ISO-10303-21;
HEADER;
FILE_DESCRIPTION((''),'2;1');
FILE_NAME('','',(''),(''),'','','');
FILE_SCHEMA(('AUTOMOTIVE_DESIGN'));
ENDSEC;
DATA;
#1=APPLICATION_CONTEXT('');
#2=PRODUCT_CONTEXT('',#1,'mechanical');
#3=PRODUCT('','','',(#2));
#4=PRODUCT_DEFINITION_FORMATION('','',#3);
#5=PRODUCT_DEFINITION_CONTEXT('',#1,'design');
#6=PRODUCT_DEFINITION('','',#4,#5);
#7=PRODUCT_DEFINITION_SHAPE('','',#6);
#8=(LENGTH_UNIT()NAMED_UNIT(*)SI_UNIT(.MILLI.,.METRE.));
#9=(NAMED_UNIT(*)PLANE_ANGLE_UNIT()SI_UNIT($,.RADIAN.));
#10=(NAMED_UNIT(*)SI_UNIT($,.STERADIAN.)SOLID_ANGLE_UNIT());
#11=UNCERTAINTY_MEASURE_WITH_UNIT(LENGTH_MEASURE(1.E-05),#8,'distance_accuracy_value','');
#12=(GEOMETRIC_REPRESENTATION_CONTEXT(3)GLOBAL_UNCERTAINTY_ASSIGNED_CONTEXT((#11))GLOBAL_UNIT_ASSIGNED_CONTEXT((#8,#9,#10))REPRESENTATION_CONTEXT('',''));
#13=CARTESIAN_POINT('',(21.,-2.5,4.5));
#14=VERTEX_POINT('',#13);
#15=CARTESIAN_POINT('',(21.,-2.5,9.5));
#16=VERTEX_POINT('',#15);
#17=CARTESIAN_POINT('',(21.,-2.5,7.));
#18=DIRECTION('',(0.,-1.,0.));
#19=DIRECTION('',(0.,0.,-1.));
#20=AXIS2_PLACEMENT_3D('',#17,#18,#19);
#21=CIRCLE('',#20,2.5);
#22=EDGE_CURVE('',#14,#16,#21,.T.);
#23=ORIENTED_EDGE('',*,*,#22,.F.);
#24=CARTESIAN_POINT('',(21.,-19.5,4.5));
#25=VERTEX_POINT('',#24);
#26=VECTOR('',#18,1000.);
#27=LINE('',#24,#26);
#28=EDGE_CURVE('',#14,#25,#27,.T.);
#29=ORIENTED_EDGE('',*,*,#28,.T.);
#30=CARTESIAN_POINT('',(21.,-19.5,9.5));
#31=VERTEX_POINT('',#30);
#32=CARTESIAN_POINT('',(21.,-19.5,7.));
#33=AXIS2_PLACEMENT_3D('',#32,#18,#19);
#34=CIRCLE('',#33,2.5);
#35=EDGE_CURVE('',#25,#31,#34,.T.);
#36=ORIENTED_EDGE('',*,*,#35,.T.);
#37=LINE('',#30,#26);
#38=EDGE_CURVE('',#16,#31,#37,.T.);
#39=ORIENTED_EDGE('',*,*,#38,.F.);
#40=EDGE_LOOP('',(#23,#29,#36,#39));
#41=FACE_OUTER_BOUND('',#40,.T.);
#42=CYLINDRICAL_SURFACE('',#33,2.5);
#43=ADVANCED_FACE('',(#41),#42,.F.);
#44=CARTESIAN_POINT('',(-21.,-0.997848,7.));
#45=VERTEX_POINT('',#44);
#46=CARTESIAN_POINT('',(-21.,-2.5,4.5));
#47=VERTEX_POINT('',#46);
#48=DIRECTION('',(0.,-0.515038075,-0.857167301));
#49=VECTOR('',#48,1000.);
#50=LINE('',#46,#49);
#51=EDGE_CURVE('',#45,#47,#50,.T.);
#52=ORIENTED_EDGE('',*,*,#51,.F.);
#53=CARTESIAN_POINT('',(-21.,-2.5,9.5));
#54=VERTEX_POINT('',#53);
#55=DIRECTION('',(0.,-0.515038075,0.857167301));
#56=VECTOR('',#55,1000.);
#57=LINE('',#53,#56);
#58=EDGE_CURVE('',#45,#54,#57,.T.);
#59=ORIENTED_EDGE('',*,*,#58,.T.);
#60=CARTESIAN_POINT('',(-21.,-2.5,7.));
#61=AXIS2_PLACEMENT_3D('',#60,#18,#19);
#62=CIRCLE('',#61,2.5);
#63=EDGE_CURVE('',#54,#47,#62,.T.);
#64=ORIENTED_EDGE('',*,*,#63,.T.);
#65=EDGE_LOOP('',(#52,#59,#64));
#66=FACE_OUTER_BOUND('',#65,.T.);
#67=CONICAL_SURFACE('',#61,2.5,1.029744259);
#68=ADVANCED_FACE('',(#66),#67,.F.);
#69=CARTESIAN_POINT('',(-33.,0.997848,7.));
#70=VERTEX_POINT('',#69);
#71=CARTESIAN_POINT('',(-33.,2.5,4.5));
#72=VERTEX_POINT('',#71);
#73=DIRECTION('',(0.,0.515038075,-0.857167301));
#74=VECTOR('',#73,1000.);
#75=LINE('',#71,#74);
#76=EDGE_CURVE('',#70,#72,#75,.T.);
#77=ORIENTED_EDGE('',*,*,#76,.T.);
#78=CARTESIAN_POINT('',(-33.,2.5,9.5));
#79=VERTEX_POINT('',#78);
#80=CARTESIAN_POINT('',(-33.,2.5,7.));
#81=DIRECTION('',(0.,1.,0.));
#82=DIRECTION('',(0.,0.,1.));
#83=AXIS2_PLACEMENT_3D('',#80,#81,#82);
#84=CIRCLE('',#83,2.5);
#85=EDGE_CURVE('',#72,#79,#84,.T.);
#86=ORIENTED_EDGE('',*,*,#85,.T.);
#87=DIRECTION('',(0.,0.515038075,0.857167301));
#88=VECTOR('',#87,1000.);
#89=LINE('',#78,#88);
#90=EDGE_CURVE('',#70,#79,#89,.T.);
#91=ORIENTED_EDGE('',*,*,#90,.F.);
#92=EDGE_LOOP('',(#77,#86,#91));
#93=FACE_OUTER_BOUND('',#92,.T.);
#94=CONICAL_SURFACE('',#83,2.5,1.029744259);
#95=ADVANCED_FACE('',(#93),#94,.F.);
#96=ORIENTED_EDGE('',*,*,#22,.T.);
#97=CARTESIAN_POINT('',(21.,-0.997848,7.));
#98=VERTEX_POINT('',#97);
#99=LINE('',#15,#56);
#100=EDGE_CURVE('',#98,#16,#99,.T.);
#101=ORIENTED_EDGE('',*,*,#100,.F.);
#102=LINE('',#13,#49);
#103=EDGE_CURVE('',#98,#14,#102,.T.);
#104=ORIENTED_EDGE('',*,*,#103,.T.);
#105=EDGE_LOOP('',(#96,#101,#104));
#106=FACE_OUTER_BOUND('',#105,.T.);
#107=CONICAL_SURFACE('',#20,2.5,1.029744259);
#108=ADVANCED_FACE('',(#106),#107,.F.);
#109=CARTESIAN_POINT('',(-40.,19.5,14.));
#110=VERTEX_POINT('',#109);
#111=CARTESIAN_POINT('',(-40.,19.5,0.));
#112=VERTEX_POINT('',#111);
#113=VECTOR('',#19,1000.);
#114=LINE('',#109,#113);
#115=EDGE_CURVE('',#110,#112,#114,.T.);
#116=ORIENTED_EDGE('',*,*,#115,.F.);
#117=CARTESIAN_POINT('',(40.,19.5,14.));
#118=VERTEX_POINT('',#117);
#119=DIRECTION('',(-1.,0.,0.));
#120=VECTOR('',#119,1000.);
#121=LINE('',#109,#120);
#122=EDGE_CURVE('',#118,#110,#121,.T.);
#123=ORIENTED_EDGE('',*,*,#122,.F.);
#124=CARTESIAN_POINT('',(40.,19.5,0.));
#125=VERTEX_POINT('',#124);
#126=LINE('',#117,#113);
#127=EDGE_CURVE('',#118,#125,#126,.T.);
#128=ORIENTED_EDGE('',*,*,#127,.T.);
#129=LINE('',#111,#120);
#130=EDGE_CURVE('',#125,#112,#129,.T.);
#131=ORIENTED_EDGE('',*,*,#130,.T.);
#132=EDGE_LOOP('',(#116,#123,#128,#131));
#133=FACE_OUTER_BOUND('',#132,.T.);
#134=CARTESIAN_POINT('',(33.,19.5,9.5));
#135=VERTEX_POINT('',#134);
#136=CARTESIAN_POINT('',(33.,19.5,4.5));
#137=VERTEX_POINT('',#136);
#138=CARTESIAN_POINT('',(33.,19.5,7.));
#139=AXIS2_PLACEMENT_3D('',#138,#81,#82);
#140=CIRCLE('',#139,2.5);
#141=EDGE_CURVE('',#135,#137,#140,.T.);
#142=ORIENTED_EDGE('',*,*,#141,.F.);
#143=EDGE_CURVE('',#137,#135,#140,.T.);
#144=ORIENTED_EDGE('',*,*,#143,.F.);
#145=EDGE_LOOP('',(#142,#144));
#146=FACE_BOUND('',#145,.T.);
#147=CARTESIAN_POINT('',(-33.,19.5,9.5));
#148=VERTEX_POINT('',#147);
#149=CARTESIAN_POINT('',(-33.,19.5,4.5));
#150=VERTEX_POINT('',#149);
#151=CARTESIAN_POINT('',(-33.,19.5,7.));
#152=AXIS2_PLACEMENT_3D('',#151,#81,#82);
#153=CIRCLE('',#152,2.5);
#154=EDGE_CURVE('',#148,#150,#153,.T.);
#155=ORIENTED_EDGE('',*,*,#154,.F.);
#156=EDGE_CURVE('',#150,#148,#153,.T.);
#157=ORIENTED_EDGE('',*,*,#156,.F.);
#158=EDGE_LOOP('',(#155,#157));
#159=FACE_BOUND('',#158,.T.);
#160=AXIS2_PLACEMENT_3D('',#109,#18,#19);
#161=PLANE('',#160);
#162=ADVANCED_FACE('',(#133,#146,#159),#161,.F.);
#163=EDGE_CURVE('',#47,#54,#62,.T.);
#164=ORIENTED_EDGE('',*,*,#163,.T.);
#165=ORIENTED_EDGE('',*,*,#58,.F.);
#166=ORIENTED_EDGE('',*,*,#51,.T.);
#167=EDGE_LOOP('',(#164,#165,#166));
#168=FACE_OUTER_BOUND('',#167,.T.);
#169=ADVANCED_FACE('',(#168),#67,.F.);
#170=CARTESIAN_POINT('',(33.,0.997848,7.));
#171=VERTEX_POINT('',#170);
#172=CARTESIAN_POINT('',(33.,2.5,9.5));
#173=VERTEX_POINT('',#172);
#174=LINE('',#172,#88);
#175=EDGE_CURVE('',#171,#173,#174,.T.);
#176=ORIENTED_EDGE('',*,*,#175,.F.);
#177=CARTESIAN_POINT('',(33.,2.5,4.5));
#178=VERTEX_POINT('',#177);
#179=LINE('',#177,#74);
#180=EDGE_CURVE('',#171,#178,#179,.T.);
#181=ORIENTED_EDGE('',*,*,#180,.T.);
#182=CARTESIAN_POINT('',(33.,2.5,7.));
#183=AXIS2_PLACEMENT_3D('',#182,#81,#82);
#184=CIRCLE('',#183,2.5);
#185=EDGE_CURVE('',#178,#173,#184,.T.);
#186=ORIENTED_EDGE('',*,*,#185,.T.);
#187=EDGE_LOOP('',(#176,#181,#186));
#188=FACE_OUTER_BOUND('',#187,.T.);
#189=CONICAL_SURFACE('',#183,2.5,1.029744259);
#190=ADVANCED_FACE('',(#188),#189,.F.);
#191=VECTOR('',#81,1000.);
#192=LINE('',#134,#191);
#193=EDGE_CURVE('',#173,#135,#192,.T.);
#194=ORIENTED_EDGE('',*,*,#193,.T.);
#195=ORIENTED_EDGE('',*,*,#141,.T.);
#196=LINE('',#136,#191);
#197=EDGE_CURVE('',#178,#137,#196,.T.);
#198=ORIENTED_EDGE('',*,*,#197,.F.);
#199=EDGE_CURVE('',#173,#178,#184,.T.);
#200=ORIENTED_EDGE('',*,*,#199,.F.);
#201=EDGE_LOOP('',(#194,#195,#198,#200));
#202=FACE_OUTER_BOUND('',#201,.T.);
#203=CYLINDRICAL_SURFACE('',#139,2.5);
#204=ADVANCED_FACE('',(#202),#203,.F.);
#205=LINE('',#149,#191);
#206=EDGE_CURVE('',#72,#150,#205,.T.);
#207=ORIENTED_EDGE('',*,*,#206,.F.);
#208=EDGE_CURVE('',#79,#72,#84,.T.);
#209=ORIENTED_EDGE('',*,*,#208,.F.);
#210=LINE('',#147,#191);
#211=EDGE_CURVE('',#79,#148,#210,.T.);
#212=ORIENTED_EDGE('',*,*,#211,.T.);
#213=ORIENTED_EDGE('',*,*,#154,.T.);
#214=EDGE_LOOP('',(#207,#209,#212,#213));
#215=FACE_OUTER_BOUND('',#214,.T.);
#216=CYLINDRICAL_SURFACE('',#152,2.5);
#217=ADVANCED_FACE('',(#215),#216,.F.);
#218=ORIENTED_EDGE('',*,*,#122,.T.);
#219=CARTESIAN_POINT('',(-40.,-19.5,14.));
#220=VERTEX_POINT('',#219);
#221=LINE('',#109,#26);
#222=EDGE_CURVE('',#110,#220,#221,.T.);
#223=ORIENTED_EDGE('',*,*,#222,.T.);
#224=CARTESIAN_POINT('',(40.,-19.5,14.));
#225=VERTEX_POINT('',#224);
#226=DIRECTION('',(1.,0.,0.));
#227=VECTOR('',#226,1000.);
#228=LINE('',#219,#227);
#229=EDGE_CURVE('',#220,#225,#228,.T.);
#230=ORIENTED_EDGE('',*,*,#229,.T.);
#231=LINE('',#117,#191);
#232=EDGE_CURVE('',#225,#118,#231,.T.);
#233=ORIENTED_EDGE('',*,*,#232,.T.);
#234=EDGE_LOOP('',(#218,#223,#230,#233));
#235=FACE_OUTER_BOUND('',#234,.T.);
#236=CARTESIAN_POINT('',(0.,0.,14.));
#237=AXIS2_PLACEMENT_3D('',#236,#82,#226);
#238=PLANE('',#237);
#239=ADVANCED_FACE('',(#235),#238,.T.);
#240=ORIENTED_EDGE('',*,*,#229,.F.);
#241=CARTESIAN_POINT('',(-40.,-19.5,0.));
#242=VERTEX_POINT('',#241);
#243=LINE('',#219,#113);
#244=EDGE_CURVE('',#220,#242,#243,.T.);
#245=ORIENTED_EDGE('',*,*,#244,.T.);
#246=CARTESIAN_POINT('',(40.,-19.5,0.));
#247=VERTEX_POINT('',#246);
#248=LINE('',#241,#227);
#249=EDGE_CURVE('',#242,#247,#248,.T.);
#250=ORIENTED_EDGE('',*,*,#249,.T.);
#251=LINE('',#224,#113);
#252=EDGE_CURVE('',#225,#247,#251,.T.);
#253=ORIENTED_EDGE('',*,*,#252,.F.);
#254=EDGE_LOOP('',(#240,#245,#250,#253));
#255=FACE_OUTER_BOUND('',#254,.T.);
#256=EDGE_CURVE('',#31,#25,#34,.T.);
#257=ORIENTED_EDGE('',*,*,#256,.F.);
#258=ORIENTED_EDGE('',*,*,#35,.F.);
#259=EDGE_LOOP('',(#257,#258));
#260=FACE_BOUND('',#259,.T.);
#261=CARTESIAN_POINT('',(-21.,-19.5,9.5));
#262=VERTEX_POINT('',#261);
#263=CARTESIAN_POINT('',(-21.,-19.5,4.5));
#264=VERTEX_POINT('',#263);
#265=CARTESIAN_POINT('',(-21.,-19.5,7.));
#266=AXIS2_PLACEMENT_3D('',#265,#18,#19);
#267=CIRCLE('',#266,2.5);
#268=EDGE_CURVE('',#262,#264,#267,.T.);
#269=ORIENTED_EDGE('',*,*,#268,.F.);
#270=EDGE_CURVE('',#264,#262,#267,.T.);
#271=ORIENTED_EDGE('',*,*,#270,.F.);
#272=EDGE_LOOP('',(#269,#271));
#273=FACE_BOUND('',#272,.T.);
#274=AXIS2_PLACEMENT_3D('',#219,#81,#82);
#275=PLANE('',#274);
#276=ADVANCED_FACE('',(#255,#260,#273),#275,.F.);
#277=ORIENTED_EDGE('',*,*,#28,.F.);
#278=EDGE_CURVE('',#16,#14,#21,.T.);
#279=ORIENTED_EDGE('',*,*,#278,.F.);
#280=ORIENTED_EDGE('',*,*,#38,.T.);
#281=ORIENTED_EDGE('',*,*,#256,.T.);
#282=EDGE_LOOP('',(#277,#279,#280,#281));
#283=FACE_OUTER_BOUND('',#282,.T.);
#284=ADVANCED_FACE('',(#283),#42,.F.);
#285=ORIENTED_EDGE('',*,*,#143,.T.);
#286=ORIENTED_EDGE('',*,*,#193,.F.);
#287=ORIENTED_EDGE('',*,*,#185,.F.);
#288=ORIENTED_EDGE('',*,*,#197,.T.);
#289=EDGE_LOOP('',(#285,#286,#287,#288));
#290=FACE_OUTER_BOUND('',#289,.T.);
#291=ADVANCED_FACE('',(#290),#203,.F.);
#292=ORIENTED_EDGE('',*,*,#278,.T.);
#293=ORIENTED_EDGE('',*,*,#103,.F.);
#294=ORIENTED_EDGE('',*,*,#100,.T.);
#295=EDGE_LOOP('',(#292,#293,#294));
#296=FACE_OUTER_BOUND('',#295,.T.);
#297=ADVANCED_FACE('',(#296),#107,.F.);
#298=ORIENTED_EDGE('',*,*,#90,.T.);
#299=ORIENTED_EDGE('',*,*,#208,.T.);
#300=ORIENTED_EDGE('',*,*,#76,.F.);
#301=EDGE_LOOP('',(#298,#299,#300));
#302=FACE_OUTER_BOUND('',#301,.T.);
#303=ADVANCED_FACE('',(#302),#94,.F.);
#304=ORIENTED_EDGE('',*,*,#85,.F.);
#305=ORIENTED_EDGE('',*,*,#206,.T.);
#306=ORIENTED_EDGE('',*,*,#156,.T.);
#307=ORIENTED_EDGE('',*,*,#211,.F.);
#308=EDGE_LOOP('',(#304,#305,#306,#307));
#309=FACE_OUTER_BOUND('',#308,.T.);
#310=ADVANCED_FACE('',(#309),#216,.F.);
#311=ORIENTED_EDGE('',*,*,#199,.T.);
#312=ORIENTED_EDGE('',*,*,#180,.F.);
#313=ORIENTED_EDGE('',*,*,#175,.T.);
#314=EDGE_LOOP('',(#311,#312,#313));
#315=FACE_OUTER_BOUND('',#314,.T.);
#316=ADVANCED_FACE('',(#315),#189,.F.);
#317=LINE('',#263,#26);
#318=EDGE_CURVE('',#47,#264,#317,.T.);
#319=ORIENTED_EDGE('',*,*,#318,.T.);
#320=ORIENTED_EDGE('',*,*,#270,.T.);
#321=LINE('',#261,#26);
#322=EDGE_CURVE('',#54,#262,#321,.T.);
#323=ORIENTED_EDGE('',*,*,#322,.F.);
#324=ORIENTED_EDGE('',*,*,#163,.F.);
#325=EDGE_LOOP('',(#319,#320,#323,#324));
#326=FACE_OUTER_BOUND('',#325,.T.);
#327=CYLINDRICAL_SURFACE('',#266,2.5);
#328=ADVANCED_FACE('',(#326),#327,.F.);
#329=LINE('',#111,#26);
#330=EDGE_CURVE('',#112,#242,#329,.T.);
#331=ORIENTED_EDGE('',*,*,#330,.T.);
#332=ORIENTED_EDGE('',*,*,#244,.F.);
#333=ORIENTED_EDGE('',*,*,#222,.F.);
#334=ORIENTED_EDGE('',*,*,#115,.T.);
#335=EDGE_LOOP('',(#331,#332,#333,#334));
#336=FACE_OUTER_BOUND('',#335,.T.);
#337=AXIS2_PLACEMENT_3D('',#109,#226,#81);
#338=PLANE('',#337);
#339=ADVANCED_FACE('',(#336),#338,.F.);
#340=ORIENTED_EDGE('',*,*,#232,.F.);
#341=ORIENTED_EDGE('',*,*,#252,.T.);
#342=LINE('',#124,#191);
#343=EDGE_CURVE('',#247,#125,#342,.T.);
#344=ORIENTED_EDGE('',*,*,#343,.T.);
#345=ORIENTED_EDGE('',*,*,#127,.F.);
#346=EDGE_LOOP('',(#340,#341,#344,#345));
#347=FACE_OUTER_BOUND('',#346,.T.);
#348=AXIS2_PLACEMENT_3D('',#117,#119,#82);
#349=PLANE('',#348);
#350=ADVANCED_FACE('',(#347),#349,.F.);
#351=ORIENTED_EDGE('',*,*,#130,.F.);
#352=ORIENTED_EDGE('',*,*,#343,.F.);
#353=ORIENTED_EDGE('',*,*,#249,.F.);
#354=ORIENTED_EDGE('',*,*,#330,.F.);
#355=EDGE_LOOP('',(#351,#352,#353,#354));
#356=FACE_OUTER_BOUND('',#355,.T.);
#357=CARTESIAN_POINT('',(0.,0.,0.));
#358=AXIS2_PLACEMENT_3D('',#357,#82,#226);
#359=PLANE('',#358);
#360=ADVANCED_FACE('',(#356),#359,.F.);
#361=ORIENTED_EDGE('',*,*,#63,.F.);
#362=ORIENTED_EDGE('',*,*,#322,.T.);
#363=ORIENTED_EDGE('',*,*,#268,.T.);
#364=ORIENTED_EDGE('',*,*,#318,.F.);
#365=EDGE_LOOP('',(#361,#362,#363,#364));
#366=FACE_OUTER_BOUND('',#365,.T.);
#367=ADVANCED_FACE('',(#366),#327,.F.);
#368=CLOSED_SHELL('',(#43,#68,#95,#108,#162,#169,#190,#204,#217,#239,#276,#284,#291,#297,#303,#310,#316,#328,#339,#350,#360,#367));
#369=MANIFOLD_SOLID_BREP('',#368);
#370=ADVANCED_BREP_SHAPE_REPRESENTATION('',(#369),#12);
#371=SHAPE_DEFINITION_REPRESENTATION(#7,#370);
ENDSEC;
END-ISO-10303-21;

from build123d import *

# Parameters (mm, degrees)
SKETCH_1_W             = 80
SKETCH_1_H             = 39
EXTRUDE_1_DEPTH        = 14
HOLE_WIZARD_M6_1_D     = 5
HOLE_WIZARD_M6_1_DEPTH = 17
HOLE_WIZARD_M6_1_TIP   = 1.502151548
HOLE_WIZARD_M6_2_D     = 5
HOLE_WIZARD_M6_2_DEPTH = 17
HOLE_WIZARD_M6_2_TIP   = 1.502151548


with BuildPart() as part:
    # 草图1 → 凸台-拉伸1 (new body)
    with BuildSketch(Plane.XY):
        Rectangle(SKETCH_1_W, SKETCH_1_H)
    extrude(amount=EXTRUDE_1_DEPTH)

    # M6 螺纹孔1
    with Locations(Plane(origin=(0, -19.5, 0), x_dir=(-1, 0, 0), z_dir=(0, -1, 0))):
        with Locations((-21, -7), (21, -7)):
            Hole(HOLE_WIZARD_M6_1_D / 2, depth=HOLE_WIZARD_M6_1_DEPTH)
            with Locations((0, 0, -(HOLE_WIZARD_M6_1_DEPTH + HOLE_WIZARD_M6_1_TIP / 2))):  # 118° drill point
                Cone(0, HOLE_WIZARD_M6_1_D / 2, HOLE_WIZARD_M6_1_TIP, mode=Mode.SUBTRACT)

    # M6 螺纹孔2
    with Locations(Plane(origin=(0, 19.5, 0), x_dir=(1, 0, 0), z_dir=(0, 1, 0))):
        with Locations((-33, -7), (33, -7)):
            Hole(HOLE_WIZARD_M6_2_D / 2, depth=HOLE_WIZARD_M6_2_DEPTH)
            with Locations((0, 0, -(HOLE_WIZARD_M6_2_DEPTH + HOLE_WIZARD_M6_2_TIP / 2))):  # 118° drill point
                Cone(0, HOLE_WIZARD_M6_2_D / 2, HOLE_WIZARD_M6_2_TIP, mode=Mode.SUBTRACT)


solid = part.part
